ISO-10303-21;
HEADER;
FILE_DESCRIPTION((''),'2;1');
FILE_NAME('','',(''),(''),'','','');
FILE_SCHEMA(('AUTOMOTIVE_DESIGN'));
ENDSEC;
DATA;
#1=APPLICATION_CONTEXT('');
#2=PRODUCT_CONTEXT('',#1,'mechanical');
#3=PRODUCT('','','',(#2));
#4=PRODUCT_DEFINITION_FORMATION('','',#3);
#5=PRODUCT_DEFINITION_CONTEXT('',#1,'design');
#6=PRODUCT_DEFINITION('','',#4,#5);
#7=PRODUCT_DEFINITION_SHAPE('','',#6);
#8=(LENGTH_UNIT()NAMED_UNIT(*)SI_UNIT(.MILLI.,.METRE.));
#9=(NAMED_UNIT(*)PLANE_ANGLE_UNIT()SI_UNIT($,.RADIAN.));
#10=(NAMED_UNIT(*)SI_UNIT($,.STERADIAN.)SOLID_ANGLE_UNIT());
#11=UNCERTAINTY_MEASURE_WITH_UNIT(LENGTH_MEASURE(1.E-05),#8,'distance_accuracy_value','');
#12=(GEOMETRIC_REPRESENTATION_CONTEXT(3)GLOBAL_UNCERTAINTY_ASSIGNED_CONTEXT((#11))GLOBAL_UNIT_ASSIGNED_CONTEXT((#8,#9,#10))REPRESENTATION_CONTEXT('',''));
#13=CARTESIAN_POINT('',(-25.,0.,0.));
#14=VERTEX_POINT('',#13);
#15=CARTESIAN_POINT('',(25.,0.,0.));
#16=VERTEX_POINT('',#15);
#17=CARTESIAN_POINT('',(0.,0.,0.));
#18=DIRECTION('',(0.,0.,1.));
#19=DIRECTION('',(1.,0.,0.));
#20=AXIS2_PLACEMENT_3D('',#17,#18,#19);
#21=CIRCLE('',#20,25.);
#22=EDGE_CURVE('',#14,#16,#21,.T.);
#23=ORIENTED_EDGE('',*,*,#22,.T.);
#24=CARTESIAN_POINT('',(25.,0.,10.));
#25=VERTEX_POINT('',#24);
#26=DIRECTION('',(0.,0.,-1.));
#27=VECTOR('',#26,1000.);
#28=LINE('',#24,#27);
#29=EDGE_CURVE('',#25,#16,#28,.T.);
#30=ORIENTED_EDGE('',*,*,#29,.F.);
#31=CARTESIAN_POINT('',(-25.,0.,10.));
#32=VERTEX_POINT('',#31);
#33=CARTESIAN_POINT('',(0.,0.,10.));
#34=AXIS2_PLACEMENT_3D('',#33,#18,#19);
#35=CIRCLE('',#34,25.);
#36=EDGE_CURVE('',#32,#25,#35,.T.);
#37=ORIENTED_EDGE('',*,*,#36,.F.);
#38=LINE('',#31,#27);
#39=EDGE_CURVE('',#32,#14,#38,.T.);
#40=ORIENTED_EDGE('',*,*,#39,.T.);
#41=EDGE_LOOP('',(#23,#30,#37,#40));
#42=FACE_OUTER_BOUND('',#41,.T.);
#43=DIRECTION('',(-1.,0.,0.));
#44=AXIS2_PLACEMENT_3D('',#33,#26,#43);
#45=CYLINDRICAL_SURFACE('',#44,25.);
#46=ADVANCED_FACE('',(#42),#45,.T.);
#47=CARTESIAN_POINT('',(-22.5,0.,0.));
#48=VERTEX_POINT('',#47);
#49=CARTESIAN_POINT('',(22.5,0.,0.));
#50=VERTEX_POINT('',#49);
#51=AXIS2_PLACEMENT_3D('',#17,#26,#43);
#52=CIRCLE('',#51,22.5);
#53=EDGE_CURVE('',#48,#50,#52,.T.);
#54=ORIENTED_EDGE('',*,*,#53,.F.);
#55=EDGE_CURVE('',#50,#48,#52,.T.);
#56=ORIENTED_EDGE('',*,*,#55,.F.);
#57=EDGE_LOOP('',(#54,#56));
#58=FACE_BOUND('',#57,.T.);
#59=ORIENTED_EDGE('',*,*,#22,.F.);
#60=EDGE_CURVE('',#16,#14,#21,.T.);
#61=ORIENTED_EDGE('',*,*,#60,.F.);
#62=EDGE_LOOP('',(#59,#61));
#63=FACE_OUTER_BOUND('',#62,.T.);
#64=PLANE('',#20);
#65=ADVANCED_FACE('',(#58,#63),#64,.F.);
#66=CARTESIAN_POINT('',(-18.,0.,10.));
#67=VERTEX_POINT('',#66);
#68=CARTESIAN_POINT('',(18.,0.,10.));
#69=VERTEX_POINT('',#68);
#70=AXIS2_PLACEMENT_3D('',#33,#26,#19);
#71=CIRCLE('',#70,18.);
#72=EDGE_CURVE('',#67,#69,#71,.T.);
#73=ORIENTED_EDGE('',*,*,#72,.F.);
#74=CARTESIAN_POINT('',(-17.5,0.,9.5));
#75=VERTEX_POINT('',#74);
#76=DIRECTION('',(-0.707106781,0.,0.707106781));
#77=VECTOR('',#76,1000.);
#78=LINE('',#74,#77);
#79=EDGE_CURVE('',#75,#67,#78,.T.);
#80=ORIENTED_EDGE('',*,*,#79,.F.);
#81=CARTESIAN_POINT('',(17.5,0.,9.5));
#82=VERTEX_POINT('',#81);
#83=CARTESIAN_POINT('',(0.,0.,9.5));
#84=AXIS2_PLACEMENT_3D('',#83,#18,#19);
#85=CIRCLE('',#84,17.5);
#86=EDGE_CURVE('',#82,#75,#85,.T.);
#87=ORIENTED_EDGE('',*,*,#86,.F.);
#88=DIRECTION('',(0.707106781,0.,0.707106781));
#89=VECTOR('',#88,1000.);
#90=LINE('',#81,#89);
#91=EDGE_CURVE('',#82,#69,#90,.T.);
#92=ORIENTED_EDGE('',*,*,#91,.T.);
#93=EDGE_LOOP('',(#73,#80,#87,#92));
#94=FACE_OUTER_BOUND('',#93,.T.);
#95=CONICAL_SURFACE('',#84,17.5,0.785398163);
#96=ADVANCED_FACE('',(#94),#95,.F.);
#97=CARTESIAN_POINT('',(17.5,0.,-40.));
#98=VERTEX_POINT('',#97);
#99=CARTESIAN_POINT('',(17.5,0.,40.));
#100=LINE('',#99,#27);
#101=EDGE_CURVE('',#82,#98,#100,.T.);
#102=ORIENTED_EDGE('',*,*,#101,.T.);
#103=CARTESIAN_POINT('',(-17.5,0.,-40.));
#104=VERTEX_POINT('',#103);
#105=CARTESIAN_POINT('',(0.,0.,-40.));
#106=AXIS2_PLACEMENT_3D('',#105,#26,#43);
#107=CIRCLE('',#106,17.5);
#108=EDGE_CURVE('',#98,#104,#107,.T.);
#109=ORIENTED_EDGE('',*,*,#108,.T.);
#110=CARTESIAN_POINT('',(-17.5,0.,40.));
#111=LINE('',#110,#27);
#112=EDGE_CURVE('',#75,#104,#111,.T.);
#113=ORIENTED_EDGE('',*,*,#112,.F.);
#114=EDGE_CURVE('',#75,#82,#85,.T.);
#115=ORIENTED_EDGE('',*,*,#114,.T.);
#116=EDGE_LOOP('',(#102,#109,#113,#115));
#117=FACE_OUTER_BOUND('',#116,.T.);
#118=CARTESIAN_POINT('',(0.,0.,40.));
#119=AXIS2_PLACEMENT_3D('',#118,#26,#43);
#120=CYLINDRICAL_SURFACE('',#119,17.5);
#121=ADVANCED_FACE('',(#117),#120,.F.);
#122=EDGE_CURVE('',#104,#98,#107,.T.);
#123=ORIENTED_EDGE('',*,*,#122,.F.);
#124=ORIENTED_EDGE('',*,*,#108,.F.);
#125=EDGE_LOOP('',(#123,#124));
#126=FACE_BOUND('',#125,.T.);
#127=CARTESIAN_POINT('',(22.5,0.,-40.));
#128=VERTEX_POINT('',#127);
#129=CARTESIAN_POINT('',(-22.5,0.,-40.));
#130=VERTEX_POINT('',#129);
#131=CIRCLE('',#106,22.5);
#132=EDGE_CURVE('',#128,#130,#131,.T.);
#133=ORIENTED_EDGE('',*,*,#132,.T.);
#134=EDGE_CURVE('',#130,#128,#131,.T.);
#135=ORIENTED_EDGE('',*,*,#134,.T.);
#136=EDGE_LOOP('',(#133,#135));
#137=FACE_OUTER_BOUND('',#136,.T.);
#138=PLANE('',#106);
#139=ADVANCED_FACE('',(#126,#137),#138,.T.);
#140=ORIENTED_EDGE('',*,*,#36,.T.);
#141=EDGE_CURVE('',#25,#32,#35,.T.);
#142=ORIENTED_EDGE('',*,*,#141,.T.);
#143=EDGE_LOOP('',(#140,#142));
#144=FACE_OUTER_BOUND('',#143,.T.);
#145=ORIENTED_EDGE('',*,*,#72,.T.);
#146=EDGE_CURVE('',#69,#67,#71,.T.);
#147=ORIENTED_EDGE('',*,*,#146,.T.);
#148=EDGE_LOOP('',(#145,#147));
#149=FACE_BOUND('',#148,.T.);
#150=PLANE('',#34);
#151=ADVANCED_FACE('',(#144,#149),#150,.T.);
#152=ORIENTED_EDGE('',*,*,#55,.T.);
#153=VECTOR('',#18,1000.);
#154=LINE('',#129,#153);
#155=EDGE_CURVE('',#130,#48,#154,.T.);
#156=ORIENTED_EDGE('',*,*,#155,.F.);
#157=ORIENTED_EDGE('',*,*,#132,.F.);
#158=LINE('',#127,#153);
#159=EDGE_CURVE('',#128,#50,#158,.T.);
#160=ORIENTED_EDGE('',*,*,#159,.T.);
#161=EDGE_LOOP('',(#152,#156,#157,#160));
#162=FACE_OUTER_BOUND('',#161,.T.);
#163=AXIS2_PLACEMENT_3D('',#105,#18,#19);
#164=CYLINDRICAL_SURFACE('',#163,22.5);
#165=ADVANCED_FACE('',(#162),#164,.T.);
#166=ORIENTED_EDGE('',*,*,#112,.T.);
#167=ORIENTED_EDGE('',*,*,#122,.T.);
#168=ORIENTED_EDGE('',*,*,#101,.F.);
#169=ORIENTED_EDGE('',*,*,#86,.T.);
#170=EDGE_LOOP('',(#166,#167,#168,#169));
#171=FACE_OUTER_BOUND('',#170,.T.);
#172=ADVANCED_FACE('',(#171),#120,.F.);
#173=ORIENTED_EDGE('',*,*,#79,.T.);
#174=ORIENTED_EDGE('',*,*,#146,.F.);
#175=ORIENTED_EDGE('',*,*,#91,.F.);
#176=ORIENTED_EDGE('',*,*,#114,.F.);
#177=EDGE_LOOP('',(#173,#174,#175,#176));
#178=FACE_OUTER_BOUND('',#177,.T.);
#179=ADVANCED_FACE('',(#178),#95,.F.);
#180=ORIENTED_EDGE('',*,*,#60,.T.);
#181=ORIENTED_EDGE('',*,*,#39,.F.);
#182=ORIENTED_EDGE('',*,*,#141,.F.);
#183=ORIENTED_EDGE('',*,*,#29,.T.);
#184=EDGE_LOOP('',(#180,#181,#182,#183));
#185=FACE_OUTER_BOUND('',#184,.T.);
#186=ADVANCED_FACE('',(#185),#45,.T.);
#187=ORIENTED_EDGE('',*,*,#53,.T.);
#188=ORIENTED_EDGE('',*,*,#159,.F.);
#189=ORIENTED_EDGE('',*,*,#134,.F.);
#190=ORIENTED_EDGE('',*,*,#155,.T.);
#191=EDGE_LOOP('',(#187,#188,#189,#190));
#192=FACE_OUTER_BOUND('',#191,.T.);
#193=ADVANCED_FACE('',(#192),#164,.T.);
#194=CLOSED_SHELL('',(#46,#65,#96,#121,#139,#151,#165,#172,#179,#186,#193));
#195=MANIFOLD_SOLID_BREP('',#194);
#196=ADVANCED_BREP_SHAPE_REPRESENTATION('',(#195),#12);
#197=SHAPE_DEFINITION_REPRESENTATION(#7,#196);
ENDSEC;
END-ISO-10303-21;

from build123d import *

# Parameters (mm, degrees)
SKETCH_1_R          = 25
EXTRUDE_1_DEPTH     = 10
SKETCH_2_R          = 22.5
EXTRUDE_2_DEPTH     = 40
SKETCH_3_R          = 17.5
CUT_EXTRUDE_1_DEPTH = 80
CHAMFER_1_SIZE      = 0.5


with BuildPart() as part:
    # 草图1 → 凸台-拉伸1 (new body)
    with BuildSketch(Plane.XY):
        Circle(SKETCH_1_R)
    extrude(amount=EXTRUDE_1_DEPTH)

    # 草图2 → 凸台-拉伸2 (add)
    with BuildSketch(Plane(origin=(0, 0, 0), x_dir=(-1, 0, 0), z_dir=(0, 0, -1))):
        Circle(SKETCH_2_R)
    extrude(amount=EXTRUDE_2_DEPTH)

    # 草图3 → 切除-拉伸1 (cut)
    with BuildSketch(Plane(origin=(0, 0, -40), x_dir=(-1, 0, 0), z_dir=(0, 0, -1))):
        Circle(SKETCH_3_R)
    extrude(amount=-CUT_EXTRUDE_1_DEPTH, mode=Mode.SUBTRACT)

    # 倒角1
    chamfer_1_edges = [part.edges().sort_by_distance(p)[0] for p in [
        (17.5, 0, 10),
    ]]
    chamfer(chamfer_1_edges, length=CHAMFER_1_SIZE)


solid = part.part
